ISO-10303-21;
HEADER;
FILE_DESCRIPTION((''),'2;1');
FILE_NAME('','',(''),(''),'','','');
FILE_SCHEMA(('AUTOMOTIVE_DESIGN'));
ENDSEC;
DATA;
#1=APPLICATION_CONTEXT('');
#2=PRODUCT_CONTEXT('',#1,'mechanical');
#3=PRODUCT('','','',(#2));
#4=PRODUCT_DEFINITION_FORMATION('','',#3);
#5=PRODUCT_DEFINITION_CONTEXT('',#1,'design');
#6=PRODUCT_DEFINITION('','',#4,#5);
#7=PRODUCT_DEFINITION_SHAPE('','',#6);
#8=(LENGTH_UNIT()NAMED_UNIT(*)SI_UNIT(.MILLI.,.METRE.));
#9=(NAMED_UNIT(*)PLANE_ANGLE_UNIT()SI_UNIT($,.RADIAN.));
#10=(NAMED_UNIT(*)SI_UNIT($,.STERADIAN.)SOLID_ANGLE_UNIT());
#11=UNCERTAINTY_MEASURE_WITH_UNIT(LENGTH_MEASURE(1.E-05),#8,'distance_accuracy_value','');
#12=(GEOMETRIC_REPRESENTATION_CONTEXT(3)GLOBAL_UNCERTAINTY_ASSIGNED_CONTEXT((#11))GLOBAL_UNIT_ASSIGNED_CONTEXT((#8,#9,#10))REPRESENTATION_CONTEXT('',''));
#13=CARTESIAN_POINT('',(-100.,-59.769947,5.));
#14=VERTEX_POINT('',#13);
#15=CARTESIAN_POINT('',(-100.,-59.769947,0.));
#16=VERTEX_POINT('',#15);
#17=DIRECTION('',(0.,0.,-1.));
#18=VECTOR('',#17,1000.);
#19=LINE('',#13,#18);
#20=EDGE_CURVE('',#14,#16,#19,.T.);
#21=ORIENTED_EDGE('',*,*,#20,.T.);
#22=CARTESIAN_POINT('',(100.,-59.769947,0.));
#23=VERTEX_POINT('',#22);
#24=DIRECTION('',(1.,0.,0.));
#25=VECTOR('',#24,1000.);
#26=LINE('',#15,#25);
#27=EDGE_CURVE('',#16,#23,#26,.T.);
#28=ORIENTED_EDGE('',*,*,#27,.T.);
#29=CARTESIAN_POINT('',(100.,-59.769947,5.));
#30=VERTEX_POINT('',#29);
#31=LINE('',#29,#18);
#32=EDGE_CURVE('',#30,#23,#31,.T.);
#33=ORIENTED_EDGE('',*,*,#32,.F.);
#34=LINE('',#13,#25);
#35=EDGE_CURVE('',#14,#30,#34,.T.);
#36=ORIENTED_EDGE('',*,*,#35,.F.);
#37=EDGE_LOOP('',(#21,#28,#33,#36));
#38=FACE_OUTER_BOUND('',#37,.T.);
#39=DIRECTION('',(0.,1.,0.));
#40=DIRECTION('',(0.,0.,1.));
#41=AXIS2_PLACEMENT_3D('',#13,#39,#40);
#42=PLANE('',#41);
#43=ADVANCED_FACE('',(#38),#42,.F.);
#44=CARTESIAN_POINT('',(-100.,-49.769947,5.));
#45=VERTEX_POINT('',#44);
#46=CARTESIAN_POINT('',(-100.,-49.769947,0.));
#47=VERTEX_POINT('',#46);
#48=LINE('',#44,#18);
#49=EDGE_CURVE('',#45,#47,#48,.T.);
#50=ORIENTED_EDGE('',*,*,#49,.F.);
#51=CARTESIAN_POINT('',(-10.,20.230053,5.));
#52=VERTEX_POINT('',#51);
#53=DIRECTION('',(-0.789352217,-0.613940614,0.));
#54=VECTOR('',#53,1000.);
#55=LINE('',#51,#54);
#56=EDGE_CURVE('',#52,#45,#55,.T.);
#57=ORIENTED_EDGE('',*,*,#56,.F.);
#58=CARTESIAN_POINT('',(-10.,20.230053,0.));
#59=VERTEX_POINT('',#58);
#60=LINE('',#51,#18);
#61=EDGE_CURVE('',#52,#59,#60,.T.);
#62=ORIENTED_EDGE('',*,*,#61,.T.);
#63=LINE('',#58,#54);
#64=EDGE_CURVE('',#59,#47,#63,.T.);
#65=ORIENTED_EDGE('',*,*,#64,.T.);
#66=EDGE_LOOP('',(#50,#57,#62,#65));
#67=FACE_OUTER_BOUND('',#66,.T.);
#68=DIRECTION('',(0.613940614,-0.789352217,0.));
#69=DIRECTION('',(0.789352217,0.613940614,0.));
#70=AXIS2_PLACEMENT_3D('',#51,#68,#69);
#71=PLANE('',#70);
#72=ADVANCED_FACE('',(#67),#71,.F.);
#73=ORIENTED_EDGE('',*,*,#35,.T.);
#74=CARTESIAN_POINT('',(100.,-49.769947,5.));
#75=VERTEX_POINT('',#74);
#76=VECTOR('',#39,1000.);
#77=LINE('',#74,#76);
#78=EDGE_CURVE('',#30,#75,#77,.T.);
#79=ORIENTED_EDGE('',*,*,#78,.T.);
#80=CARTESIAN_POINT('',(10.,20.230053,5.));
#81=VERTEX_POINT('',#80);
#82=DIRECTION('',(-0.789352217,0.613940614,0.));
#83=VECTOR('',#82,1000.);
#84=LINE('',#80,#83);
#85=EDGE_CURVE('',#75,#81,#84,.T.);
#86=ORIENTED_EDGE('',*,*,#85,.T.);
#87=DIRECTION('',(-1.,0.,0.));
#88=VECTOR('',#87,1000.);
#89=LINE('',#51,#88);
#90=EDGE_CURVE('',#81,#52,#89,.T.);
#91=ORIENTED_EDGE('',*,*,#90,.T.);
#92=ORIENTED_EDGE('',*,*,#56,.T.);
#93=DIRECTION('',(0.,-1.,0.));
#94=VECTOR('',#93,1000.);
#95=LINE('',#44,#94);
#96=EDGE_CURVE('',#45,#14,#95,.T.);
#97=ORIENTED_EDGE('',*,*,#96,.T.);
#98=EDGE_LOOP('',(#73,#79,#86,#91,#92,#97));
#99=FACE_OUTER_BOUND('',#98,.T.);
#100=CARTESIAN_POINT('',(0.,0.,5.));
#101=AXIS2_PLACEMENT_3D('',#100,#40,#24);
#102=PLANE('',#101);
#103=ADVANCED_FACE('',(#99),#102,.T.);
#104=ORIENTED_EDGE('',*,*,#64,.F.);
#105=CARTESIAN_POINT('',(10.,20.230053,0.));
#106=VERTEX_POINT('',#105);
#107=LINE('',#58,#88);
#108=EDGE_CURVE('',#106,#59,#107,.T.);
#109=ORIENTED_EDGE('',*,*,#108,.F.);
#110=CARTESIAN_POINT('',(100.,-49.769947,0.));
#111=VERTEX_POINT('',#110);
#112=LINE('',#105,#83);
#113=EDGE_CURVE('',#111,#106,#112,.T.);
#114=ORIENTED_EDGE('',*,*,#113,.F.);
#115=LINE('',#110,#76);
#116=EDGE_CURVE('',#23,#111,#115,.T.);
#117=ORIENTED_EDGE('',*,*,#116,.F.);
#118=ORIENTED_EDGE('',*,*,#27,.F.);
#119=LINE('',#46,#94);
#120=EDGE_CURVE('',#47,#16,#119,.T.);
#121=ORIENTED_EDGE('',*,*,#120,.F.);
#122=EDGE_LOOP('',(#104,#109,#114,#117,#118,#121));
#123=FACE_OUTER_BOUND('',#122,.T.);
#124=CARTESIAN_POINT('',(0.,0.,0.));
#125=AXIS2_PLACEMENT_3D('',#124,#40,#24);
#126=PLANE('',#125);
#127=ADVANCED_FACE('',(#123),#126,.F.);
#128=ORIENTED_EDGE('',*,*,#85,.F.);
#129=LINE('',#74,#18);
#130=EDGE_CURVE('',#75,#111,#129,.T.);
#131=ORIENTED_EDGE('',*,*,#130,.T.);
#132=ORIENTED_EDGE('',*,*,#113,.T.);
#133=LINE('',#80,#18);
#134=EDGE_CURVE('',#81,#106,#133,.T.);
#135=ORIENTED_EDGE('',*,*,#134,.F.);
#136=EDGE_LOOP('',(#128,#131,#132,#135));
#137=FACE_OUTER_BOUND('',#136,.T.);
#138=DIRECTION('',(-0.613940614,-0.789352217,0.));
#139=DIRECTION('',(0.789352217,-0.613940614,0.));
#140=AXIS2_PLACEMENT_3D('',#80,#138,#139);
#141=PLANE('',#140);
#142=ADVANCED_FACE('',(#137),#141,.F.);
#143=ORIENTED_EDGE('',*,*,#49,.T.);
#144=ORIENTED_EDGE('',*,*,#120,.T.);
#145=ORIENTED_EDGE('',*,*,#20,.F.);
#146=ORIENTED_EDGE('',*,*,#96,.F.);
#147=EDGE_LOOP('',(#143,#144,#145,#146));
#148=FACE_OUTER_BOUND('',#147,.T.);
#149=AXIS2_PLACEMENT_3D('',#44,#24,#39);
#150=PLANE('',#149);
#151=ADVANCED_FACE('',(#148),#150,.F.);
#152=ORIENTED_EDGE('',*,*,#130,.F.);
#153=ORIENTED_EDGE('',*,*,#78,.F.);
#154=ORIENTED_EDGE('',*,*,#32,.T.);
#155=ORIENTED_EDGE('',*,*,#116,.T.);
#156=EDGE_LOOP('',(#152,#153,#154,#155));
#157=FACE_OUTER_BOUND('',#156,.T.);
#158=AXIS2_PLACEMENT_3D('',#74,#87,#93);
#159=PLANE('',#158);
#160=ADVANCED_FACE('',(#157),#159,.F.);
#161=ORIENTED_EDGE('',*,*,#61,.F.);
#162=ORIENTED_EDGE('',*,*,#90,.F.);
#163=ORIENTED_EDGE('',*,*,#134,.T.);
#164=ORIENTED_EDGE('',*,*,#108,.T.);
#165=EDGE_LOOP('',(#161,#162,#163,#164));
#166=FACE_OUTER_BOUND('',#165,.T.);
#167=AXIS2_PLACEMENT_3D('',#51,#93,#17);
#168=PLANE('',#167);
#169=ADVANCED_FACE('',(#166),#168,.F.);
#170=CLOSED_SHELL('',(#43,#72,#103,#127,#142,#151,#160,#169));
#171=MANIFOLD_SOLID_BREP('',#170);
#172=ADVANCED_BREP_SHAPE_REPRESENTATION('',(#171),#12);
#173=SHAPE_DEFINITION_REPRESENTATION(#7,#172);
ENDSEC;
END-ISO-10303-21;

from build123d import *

# Parameters (mm, degrees)
EXTRUDE_1_DEPTH = 5


with BuildPart() as part:
    # 草图1 → 凸台-拉伸1 (new body)
    with BuildSketch(Plane.XY):
        Polygon((-10, 20.230052867), (-100, -49.769947133), (-100, -59.769947133), (100, -59.769947133), (100, -49.769947133), (10, 20.230052867), align=None)
    extrude(amount=EXTRUDE_1_DEPTH)


solid = part.part
